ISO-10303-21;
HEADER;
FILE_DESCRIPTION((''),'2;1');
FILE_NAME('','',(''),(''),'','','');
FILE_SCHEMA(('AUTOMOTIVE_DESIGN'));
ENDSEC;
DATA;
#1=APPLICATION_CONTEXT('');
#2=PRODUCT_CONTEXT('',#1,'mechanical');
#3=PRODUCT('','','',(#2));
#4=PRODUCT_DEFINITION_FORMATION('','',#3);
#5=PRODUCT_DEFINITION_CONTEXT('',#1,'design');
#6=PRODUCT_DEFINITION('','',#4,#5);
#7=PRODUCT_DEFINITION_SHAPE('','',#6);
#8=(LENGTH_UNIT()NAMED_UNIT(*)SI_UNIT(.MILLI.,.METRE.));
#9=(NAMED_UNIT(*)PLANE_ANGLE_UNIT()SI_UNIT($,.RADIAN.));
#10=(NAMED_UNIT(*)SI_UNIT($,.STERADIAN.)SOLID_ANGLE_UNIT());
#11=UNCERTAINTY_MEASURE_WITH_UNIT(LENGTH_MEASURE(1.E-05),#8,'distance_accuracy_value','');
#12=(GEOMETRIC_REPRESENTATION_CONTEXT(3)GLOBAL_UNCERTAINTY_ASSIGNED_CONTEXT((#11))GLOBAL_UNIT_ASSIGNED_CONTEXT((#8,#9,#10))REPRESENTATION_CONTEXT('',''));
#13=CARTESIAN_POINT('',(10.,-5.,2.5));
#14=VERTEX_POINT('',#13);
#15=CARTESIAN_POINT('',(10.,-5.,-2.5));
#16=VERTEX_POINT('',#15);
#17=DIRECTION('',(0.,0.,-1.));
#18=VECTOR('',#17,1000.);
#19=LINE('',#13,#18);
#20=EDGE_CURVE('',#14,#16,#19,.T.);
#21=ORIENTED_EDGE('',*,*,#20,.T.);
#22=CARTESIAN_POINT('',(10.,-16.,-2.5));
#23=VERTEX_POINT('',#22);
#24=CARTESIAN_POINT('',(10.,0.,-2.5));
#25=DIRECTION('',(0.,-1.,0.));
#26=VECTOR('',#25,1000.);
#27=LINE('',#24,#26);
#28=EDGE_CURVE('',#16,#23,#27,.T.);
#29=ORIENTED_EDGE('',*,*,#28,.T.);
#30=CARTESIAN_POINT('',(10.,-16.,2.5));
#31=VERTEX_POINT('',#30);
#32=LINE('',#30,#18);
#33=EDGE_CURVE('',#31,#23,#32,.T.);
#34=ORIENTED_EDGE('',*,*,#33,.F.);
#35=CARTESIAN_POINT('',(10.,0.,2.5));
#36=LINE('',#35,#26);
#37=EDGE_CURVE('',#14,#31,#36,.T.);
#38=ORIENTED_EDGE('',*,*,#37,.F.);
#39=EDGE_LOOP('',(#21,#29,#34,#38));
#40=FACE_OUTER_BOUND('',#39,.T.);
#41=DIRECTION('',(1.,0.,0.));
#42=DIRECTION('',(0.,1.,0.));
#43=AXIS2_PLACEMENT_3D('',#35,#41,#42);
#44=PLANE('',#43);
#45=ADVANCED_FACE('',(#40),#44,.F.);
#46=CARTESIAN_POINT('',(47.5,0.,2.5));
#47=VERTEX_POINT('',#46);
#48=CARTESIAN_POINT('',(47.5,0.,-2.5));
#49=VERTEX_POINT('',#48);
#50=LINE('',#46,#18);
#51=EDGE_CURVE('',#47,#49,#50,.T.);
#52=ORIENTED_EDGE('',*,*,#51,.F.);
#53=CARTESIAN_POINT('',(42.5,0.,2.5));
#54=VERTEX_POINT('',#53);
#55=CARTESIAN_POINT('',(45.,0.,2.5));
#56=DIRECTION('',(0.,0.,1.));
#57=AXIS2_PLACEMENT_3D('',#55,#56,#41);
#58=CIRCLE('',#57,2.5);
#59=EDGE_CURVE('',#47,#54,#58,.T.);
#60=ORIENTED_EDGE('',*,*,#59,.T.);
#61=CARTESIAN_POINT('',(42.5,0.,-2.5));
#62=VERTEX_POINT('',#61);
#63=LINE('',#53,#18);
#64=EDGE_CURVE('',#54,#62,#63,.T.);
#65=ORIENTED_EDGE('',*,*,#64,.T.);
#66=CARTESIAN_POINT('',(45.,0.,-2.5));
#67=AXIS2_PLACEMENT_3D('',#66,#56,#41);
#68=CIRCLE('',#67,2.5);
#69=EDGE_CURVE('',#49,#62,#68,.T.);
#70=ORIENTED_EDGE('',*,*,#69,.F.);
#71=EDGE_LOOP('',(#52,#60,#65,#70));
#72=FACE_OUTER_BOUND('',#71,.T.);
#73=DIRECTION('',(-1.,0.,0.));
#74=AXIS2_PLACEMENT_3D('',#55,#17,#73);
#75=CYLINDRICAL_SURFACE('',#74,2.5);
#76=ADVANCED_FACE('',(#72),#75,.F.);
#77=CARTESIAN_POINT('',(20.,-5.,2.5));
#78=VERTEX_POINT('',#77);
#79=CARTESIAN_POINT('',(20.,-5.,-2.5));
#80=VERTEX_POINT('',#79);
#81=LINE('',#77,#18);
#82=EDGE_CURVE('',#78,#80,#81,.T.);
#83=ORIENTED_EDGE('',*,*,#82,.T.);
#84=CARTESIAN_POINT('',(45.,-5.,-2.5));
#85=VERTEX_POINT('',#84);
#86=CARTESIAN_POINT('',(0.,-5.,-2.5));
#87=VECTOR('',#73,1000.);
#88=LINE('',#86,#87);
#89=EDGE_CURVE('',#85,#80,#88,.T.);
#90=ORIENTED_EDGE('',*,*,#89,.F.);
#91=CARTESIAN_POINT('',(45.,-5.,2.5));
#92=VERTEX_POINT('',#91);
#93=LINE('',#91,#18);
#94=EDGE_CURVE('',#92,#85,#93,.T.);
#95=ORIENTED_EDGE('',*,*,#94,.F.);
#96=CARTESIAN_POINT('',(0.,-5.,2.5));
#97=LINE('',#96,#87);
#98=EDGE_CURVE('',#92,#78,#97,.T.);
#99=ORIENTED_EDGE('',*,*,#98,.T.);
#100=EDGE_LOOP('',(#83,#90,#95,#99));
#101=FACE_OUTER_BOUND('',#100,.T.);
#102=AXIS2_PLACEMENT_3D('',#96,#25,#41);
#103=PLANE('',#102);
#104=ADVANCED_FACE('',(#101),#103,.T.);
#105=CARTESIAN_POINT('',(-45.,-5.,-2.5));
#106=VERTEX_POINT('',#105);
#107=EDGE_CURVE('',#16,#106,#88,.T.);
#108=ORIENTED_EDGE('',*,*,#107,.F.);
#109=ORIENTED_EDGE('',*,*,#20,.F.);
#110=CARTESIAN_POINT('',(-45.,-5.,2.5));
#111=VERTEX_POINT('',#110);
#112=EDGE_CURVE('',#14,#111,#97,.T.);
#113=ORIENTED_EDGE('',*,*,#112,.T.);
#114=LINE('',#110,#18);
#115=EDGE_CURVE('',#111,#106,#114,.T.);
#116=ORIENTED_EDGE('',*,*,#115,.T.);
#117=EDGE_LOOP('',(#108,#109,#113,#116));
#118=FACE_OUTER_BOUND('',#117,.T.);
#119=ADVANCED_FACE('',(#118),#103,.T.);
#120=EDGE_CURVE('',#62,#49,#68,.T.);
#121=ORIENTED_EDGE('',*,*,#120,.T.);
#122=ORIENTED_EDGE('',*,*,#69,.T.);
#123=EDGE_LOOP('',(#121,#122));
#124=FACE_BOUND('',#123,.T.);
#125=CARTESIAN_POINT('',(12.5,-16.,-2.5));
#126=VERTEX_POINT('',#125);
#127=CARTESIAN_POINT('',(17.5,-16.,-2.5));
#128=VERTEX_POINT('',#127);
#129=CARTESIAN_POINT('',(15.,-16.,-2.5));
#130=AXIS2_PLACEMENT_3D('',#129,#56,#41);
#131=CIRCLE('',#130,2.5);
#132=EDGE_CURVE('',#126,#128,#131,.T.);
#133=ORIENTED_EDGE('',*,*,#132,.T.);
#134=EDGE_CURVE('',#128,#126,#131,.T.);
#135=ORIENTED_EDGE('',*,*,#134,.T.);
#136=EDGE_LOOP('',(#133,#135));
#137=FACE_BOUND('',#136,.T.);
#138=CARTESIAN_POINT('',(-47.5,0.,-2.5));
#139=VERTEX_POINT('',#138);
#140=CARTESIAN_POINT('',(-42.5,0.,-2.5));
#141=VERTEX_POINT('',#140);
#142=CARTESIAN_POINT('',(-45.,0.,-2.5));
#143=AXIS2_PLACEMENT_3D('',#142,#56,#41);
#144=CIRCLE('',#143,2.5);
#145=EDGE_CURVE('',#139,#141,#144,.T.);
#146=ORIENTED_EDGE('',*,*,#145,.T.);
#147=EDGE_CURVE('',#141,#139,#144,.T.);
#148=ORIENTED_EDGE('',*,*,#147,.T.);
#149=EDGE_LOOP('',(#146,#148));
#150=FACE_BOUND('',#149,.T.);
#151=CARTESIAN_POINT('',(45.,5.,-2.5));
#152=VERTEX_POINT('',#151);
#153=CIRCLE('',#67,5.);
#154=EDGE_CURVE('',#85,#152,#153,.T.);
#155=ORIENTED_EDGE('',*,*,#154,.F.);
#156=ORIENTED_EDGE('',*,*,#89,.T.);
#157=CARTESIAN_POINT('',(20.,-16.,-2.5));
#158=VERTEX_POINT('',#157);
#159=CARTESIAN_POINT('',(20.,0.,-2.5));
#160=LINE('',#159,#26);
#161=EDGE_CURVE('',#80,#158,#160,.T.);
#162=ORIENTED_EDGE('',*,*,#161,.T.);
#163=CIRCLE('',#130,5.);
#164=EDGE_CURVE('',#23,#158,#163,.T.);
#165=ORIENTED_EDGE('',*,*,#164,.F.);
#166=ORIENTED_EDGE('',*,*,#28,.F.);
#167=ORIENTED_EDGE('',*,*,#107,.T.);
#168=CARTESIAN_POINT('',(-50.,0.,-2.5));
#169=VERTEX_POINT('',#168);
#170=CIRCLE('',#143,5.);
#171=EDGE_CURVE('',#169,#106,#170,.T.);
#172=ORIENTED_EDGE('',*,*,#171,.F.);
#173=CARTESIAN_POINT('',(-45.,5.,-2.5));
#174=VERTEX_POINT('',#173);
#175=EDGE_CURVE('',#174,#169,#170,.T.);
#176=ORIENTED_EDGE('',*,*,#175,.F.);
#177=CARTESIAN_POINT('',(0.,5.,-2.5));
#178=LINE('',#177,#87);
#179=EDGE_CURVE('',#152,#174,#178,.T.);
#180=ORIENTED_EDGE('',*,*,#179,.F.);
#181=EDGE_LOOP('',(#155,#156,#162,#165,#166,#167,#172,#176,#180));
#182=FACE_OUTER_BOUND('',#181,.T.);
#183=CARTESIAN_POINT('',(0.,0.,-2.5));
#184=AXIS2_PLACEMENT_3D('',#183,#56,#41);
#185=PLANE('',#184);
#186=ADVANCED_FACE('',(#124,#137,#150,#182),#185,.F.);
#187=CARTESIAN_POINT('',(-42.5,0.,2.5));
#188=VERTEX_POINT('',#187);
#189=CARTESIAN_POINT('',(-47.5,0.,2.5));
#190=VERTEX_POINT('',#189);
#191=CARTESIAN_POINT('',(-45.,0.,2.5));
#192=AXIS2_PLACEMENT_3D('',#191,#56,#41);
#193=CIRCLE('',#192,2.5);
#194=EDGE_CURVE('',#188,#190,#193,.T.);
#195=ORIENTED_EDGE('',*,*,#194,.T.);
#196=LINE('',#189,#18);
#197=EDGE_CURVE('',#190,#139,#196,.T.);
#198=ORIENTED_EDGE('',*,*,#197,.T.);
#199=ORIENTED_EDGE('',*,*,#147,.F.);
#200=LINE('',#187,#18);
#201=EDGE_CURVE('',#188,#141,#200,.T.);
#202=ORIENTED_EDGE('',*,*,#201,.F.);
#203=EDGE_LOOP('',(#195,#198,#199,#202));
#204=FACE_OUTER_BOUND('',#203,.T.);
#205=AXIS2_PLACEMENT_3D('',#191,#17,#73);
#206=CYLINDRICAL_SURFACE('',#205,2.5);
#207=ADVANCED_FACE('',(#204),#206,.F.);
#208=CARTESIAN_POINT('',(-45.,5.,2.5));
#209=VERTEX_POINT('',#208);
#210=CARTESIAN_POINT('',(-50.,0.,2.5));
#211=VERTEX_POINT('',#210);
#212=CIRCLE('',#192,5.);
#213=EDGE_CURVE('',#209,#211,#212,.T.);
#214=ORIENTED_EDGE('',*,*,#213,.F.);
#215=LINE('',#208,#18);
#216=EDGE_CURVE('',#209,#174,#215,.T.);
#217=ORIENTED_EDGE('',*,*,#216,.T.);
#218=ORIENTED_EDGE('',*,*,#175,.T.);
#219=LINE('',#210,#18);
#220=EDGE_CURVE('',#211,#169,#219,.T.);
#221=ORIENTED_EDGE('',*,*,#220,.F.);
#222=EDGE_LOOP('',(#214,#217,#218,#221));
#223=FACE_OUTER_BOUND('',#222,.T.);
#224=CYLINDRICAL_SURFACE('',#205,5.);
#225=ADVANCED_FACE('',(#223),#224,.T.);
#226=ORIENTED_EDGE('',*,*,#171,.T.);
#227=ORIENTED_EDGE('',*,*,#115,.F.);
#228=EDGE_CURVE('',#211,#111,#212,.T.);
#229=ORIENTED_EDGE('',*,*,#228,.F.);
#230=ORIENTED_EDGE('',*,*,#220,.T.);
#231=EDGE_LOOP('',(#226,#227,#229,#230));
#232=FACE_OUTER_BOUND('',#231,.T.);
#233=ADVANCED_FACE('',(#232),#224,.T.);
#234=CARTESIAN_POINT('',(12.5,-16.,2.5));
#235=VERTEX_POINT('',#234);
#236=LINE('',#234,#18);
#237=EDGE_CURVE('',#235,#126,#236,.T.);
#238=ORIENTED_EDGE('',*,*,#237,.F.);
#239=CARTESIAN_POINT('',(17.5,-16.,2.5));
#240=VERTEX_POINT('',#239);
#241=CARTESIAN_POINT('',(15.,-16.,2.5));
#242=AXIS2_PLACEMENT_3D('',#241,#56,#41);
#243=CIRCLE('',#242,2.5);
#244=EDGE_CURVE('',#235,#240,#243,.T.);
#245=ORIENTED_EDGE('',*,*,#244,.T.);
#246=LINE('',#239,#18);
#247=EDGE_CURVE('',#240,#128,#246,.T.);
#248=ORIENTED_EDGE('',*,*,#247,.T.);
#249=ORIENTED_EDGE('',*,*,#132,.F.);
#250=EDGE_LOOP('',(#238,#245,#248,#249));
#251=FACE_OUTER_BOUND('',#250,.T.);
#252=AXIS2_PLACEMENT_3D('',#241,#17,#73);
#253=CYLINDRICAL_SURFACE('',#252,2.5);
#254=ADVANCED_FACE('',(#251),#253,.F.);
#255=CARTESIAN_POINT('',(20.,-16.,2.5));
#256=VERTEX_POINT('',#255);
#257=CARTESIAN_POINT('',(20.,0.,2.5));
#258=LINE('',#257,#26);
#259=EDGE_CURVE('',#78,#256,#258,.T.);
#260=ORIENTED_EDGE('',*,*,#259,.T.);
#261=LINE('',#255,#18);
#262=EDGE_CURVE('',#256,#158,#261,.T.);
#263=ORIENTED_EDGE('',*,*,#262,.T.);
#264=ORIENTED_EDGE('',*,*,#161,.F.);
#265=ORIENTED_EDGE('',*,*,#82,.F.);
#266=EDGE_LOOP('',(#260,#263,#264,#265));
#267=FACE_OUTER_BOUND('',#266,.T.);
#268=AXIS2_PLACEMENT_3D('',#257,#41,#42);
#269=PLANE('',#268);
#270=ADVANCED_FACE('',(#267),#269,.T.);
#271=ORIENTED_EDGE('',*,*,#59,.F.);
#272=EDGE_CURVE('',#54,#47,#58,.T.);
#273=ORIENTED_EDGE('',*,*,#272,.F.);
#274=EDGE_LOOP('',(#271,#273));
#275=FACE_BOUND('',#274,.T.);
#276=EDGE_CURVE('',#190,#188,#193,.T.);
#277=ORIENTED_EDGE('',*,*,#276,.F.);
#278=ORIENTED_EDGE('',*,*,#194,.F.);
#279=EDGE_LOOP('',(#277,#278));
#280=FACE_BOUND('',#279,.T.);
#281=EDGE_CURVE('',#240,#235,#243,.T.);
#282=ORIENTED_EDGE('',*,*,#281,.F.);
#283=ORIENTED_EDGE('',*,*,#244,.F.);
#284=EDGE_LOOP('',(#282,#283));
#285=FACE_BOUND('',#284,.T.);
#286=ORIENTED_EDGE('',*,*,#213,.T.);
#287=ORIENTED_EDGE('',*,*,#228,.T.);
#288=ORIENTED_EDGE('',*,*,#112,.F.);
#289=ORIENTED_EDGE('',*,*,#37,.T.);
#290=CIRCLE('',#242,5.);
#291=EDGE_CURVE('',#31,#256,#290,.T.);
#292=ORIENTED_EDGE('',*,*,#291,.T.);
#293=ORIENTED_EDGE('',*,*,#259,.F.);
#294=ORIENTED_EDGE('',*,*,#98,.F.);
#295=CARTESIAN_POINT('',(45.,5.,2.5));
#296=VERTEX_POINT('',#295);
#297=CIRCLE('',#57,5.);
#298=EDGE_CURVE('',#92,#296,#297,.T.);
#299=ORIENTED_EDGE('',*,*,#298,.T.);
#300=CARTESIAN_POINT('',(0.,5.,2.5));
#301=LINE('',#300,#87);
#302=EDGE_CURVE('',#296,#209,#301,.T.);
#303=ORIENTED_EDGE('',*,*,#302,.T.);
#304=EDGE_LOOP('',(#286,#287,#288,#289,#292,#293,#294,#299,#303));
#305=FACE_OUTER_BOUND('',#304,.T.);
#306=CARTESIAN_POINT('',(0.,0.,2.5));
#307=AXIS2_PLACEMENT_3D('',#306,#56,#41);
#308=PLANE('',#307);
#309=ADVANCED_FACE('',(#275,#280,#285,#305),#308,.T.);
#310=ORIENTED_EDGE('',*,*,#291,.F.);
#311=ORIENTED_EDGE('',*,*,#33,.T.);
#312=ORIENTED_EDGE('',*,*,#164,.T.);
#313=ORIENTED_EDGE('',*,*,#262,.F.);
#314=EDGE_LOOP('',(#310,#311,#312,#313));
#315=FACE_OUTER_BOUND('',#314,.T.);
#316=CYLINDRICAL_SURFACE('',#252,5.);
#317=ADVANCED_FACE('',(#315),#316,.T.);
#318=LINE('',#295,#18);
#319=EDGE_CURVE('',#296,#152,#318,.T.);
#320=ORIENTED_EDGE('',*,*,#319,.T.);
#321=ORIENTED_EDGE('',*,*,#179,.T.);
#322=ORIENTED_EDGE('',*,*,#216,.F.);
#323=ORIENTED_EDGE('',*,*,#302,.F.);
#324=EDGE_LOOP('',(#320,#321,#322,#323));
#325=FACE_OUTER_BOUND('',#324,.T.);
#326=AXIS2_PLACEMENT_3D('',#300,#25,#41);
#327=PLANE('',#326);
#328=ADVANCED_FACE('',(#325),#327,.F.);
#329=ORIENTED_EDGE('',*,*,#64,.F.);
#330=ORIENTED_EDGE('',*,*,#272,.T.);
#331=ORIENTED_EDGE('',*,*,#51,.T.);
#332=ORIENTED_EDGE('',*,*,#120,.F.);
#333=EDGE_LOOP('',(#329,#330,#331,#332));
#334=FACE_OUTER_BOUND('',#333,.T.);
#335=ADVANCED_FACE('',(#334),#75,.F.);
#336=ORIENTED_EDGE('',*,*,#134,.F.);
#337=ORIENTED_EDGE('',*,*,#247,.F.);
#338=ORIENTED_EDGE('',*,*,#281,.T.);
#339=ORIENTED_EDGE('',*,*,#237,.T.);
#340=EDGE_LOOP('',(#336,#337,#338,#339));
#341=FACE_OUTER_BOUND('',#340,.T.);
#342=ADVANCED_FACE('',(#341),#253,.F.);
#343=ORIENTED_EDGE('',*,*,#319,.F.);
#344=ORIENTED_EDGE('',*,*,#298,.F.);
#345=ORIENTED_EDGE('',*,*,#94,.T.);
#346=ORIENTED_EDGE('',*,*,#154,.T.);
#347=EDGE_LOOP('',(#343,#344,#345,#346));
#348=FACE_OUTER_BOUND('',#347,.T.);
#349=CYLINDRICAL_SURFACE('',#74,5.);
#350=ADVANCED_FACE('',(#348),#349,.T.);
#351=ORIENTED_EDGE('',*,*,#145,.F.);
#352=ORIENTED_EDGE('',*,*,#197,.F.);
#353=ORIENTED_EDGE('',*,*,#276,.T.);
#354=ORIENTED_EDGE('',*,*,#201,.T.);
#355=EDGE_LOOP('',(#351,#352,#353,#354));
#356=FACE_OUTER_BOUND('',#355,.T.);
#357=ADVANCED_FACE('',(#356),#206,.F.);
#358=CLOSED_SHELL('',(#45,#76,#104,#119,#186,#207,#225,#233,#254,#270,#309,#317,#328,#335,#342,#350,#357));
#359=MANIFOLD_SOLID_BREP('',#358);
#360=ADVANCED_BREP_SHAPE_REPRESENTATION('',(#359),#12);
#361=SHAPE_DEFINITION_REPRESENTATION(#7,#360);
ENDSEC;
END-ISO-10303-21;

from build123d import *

# Parameters (mm, degrees)
LINK_PLATE_PROFILE_R = 2.5
LINK_PLATE_PROFILE_W = 10
LINK_PLATE_PROFILE_H = 10
LINK_PLATE_5MM_DEPTH = 2.5


with BuildPart() as part:
    # Link Plate Profile → Link Plate 5mm (new, symmetric)
    # profile 1 of 4: a face of its own
    with BuildSketch(Plane.XY):
        with BuildLine():
            Line((-45, -5), (10, -5))
            Line((10, -5), (10, 5))
            Line((10, 5), (-45, 5))
            ThreePointArc((-45, 5), (-50, 0), (-45, -5))
        make_face()
        with Locations((-45, 0)):
            Circle(LINK_PLATE_PROFILE_R, mode=Mode.SUBTRACT)
    # profile 2 of 4: a face of its own
    with BuildSketch(Plane.XY):
        with Locations((15, 0)):
            Rectangle(LINK_PLATE_PROFILE_W, LINK_PLATE_PROFILE_H)
    # profile 3 of 4: a face of its own
    with BuildSketch(Plane.XY):
        with BuildLine():
            Line((20, -5), (45, -5))
            ThreePointArc((45, -5), (50, 0), (45, 5))
            Line((45, 5), (20, 5))
            Line((20, 5), (20, -5))
        make_face()
        with Locations((45, 0)):
            Circle(LINK_PLATE_PROFILE_R, mode=Mode.SUBTRACT)
    # profile 4 of 4: a face of its own
    with BuildSketch(Plane.XY):
        with BuildLine():
            Line((20, -16), (20, -5))
            Line((20, -5), (10, -5))
            Line((10, -5), (10, -16))
            ThreePointArc((10, -16), (15, -21), (20, -16))
        make_face()
        with Locations((15, -16)):
            Circle(LINK_PLATE_PROFILE_R, mode=Mode.SUBTRACT)
    extrude(amount=LINK_PLATE_5MM_DEPTH, both=True)


solid = part.part
